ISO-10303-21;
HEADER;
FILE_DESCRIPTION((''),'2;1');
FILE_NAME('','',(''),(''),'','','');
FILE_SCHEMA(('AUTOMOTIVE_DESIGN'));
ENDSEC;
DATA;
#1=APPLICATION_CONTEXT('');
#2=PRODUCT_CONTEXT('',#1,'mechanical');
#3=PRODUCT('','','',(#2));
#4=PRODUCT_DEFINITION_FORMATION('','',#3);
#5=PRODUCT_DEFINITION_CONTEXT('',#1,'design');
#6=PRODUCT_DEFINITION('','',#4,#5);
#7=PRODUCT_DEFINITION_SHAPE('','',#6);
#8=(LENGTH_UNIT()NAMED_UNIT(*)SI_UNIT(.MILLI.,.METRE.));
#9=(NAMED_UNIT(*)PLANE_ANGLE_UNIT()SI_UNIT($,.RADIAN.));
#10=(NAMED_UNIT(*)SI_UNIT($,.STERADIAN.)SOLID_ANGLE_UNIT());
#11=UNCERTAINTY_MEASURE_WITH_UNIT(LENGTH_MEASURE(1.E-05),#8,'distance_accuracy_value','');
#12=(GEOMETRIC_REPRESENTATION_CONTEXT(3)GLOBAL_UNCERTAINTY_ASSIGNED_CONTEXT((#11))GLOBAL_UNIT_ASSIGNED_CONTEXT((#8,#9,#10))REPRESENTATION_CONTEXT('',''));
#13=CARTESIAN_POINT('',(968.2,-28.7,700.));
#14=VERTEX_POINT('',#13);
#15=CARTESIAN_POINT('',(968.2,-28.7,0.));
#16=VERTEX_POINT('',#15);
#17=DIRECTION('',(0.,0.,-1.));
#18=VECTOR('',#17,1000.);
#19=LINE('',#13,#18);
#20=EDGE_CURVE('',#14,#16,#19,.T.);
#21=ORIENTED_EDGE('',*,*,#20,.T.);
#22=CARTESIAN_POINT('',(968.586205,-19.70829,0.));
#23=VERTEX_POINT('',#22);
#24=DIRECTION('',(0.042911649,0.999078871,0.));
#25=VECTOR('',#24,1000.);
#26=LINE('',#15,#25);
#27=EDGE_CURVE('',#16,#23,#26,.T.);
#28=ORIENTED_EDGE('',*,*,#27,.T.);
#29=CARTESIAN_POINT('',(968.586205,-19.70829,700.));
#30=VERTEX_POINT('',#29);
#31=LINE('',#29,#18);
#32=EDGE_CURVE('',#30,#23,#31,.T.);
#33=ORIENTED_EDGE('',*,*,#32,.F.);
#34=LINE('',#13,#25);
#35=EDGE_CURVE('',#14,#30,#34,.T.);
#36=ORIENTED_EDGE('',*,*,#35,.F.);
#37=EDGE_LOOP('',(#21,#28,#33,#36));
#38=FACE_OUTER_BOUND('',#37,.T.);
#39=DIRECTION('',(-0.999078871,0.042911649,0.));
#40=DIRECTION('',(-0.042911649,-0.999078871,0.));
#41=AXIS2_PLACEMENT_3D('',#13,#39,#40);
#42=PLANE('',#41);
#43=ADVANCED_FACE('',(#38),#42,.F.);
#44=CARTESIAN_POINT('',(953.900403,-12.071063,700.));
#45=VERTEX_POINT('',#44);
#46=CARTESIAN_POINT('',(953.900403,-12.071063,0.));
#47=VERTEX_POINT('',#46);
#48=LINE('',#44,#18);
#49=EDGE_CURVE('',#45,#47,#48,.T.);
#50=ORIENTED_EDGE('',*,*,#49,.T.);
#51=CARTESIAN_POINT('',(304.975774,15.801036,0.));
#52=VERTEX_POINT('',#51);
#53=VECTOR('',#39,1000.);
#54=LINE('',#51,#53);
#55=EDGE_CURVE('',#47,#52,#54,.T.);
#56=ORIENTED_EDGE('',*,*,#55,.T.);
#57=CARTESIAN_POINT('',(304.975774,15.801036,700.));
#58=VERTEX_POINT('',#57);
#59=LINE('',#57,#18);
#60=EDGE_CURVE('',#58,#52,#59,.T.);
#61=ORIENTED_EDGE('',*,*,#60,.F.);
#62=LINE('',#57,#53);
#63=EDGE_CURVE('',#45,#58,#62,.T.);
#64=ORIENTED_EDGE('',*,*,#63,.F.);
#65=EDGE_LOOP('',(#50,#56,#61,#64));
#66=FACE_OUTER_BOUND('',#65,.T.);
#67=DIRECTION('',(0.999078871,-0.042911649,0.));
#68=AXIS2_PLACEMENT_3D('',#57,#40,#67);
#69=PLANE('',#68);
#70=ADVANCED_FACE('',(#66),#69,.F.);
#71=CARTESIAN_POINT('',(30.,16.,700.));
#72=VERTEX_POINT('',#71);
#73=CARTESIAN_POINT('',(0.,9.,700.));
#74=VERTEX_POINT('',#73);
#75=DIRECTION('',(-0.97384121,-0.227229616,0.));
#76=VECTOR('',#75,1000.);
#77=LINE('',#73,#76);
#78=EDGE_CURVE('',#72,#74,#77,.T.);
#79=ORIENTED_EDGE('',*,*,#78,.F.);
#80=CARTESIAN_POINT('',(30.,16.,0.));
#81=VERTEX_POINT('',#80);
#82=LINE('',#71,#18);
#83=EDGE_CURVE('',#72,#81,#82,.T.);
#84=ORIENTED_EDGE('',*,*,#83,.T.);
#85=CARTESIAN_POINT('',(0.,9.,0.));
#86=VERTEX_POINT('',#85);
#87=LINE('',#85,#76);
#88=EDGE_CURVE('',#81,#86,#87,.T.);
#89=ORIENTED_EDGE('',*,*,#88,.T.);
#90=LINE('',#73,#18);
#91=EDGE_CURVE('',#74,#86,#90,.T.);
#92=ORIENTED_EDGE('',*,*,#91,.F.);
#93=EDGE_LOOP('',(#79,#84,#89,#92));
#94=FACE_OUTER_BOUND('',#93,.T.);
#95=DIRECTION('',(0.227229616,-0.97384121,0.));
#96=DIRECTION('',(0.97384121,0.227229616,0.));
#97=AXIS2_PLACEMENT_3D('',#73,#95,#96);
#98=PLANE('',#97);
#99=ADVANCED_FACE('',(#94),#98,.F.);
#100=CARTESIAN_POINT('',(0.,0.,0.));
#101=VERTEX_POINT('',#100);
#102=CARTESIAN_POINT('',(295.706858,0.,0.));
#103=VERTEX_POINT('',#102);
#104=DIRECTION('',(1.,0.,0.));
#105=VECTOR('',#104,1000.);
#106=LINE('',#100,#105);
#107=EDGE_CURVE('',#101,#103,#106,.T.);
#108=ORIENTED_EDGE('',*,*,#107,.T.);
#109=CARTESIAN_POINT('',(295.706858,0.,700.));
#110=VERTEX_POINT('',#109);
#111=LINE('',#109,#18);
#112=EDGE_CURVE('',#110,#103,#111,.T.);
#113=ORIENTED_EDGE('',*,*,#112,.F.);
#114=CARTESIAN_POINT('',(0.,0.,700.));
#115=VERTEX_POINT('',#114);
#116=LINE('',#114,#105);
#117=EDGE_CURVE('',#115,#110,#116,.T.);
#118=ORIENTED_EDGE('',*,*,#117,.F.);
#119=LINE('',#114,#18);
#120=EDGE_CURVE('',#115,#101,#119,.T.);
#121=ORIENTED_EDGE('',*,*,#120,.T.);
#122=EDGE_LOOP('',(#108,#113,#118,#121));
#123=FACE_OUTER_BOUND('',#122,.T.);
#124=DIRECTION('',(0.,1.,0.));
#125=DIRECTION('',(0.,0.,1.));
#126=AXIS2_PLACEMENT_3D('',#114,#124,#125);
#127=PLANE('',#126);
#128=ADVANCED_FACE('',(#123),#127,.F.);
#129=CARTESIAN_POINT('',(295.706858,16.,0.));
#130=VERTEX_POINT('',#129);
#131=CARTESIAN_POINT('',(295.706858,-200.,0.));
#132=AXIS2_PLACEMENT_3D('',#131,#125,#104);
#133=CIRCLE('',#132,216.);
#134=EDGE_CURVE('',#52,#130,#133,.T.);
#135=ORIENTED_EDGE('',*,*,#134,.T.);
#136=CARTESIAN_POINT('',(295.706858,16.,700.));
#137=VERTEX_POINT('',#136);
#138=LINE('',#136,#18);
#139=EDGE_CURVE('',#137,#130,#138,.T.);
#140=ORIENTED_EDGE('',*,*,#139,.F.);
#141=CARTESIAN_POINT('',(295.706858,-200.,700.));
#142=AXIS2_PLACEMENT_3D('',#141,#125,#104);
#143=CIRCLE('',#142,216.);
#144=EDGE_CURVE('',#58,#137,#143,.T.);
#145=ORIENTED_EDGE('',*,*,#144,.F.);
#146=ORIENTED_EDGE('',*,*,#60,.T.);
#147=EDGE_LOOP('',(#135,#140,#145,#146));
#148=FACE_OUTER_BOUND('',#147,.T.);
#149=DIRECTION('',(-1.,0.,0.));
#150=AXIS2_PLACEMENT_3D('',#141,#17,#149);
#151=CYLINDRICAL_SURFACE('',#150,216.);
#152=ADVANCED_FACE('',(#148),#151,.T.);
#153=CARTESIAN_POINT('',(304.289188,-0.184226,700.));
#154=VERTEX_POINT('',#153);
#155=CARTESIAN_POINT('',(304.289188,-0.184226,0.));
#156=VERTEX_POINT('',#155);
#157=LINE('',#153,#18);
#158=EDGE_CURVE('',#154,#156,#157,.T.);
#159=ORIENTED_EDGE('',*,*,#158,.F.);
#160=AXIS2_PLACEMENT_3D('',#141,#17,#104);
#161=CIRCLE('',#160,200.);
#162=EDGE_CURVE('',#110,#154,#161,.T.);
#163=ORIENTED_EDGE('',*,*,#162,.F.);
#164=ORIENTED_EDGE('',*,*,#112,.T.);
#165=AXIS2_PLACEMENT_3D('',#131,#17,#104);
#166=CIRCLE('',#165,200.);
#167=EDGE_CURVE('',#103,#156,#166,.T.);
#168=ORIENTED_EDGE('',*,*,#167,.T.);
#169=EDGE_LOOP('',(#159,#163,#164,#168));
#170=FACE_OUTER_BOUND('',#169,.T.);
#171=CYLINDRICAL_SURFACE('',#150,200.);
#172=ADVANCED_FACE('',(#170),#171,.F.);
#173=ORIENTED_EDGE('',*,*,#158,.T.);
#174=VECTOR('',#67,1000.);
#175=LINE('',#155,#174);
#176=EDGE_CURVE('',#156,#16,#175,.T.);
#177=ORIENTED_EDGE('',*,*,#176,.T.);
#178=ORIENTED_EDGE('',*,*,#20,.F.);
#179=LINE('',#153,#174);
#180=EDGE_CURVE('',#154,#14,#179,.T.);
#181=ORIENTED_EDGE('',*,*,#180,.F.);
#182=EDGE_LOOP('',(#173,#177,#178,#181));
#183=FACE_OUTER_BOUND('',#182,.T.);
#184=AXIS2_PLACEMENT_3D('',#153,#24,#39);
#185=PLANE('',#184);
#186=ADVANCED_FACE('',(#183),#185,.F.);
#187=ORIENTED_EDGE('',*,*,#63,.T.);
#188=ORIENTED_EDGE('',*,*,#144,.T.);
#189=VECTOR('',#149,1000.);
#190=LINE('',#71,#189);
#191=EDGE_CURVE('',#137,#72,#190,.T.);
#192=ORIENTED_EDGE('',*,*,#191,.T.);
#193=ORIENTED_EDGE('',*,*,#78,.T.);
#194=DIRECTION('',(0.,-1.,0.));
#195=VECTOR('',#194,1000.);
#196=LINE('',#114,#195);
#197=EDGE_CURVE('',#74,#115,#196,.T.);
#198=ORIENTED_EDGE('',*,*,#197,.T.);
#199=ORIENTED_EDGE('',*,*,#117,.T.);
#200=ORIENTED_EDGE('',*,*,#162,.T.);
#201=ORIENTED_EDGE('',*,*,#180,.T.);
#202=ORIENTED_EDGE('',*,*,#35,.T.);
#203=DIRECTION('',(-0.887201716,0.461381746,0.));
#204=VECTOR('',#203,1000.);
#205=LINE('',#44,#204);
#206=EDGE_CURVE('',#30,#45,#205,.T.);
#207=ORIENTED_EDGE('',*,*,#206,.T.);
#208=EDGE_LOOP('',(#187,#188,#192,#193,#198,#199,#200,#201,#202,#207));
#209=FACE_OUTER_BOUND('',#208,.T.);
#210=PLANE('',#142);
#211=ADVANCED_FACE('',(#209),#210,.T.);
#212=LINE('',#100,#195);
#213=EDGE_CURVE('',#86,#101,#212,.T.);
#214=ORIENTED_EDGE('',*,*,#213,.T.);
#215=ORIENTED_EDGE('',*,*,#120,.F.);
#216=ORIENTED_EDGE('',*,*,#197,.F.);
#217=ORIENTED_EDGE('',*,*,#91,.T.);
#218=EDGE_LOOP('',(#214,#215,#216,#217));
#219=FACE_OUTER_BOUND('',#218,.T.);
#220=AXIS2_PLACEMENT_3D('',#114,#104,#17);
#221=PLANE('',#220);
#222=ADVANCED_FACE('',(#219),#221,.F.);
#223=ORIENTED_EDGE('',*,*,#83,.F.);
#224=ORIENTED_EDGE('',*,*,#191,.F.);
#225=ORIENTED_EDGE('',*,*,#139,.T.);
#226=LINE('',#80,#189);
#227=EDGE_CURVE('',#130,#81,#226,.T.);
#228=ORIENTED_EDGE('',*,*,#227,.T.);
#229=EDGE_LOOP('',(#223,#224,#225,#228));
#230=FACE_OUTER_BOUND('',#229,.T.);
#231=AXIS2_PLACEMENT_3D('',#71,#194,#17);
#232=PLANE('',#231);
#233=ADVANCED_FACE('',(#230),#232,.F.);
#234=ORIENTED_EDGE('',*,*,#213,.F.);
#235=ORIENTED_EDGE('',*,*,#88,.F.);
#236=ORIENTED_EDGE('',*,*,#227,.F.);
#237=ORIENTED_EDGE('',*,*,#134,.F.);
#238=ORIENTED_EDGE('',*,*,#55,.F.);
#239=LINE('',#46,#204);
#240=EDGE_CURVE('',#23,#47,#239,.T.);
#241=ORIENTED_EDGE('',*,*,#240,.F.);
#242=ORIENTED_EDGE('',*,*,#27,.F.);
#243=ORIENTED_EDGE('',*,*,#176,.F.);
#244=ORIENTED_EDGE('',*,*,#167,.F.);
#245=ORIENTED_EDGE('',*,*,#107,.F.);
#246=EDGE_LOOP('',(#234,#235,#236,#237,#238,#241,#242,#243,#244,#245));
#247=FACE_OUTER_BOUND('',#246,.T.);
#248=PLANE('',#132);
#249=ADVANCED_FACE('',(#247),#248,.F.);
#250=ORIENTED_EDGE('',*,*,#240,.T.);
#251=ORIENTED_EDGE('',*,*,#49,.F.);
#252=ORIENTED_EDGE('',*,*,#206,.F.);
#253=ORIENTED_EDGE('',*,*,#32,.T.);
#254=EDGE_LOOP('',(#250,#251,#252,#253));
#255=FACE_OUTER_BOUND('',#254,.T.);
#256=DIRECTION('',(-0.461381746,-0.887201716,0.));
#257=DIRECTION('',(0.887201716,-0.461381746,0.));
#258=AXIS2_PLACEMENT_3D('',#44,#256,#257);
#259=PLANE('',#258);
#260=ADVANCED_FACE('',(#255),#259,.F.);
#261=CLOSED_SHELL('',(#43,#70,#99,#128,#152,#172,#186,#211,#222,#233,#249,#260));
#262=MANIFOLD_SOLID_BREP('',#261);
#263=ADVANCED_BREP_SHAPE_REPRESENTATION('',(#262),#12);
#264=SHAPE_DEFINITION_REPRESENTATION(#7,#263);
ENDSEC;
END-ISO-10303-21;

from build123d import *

# Parameters (mm, degrees)
BOSS_EXTRUDE1_DEPTH = 700


with BuildPart() as part:
    # Sketch1 → Boss-Extrude1 (new body)
    with BuildSketch(Plane.XY):
        with BuildLine():
            Line((0, 0), (295.706857871, 0))
            ThreePointArc((295.706857871, 0), (299.999011252, -0.046061756), (304.289187591, -0.184225806))
            Line((304.289187591, -0.184225806), (968.2, -28.7))
            Line((968.2, -28.7), (968.586204837, -19.708290161))
            Line((968.586204837, -19.708290161), (953.900403313, -12.071063335))
            Line((953.900403313, -12.071063335), (304.975773969, 15.801036129))
            ThreePointArc((304.975773969, 15.801036129), (300.342383522, 15.950253304), (295.706857871, 16))
            Line((295.706857871, 16), (30, 16))
            Line((30, 16), (0, 9))
            Line((0, 9), (0, 0))
        make_face()
    extrude(amount=BOSS_EXTRUDE1_DEPTH)


solid = part.part
